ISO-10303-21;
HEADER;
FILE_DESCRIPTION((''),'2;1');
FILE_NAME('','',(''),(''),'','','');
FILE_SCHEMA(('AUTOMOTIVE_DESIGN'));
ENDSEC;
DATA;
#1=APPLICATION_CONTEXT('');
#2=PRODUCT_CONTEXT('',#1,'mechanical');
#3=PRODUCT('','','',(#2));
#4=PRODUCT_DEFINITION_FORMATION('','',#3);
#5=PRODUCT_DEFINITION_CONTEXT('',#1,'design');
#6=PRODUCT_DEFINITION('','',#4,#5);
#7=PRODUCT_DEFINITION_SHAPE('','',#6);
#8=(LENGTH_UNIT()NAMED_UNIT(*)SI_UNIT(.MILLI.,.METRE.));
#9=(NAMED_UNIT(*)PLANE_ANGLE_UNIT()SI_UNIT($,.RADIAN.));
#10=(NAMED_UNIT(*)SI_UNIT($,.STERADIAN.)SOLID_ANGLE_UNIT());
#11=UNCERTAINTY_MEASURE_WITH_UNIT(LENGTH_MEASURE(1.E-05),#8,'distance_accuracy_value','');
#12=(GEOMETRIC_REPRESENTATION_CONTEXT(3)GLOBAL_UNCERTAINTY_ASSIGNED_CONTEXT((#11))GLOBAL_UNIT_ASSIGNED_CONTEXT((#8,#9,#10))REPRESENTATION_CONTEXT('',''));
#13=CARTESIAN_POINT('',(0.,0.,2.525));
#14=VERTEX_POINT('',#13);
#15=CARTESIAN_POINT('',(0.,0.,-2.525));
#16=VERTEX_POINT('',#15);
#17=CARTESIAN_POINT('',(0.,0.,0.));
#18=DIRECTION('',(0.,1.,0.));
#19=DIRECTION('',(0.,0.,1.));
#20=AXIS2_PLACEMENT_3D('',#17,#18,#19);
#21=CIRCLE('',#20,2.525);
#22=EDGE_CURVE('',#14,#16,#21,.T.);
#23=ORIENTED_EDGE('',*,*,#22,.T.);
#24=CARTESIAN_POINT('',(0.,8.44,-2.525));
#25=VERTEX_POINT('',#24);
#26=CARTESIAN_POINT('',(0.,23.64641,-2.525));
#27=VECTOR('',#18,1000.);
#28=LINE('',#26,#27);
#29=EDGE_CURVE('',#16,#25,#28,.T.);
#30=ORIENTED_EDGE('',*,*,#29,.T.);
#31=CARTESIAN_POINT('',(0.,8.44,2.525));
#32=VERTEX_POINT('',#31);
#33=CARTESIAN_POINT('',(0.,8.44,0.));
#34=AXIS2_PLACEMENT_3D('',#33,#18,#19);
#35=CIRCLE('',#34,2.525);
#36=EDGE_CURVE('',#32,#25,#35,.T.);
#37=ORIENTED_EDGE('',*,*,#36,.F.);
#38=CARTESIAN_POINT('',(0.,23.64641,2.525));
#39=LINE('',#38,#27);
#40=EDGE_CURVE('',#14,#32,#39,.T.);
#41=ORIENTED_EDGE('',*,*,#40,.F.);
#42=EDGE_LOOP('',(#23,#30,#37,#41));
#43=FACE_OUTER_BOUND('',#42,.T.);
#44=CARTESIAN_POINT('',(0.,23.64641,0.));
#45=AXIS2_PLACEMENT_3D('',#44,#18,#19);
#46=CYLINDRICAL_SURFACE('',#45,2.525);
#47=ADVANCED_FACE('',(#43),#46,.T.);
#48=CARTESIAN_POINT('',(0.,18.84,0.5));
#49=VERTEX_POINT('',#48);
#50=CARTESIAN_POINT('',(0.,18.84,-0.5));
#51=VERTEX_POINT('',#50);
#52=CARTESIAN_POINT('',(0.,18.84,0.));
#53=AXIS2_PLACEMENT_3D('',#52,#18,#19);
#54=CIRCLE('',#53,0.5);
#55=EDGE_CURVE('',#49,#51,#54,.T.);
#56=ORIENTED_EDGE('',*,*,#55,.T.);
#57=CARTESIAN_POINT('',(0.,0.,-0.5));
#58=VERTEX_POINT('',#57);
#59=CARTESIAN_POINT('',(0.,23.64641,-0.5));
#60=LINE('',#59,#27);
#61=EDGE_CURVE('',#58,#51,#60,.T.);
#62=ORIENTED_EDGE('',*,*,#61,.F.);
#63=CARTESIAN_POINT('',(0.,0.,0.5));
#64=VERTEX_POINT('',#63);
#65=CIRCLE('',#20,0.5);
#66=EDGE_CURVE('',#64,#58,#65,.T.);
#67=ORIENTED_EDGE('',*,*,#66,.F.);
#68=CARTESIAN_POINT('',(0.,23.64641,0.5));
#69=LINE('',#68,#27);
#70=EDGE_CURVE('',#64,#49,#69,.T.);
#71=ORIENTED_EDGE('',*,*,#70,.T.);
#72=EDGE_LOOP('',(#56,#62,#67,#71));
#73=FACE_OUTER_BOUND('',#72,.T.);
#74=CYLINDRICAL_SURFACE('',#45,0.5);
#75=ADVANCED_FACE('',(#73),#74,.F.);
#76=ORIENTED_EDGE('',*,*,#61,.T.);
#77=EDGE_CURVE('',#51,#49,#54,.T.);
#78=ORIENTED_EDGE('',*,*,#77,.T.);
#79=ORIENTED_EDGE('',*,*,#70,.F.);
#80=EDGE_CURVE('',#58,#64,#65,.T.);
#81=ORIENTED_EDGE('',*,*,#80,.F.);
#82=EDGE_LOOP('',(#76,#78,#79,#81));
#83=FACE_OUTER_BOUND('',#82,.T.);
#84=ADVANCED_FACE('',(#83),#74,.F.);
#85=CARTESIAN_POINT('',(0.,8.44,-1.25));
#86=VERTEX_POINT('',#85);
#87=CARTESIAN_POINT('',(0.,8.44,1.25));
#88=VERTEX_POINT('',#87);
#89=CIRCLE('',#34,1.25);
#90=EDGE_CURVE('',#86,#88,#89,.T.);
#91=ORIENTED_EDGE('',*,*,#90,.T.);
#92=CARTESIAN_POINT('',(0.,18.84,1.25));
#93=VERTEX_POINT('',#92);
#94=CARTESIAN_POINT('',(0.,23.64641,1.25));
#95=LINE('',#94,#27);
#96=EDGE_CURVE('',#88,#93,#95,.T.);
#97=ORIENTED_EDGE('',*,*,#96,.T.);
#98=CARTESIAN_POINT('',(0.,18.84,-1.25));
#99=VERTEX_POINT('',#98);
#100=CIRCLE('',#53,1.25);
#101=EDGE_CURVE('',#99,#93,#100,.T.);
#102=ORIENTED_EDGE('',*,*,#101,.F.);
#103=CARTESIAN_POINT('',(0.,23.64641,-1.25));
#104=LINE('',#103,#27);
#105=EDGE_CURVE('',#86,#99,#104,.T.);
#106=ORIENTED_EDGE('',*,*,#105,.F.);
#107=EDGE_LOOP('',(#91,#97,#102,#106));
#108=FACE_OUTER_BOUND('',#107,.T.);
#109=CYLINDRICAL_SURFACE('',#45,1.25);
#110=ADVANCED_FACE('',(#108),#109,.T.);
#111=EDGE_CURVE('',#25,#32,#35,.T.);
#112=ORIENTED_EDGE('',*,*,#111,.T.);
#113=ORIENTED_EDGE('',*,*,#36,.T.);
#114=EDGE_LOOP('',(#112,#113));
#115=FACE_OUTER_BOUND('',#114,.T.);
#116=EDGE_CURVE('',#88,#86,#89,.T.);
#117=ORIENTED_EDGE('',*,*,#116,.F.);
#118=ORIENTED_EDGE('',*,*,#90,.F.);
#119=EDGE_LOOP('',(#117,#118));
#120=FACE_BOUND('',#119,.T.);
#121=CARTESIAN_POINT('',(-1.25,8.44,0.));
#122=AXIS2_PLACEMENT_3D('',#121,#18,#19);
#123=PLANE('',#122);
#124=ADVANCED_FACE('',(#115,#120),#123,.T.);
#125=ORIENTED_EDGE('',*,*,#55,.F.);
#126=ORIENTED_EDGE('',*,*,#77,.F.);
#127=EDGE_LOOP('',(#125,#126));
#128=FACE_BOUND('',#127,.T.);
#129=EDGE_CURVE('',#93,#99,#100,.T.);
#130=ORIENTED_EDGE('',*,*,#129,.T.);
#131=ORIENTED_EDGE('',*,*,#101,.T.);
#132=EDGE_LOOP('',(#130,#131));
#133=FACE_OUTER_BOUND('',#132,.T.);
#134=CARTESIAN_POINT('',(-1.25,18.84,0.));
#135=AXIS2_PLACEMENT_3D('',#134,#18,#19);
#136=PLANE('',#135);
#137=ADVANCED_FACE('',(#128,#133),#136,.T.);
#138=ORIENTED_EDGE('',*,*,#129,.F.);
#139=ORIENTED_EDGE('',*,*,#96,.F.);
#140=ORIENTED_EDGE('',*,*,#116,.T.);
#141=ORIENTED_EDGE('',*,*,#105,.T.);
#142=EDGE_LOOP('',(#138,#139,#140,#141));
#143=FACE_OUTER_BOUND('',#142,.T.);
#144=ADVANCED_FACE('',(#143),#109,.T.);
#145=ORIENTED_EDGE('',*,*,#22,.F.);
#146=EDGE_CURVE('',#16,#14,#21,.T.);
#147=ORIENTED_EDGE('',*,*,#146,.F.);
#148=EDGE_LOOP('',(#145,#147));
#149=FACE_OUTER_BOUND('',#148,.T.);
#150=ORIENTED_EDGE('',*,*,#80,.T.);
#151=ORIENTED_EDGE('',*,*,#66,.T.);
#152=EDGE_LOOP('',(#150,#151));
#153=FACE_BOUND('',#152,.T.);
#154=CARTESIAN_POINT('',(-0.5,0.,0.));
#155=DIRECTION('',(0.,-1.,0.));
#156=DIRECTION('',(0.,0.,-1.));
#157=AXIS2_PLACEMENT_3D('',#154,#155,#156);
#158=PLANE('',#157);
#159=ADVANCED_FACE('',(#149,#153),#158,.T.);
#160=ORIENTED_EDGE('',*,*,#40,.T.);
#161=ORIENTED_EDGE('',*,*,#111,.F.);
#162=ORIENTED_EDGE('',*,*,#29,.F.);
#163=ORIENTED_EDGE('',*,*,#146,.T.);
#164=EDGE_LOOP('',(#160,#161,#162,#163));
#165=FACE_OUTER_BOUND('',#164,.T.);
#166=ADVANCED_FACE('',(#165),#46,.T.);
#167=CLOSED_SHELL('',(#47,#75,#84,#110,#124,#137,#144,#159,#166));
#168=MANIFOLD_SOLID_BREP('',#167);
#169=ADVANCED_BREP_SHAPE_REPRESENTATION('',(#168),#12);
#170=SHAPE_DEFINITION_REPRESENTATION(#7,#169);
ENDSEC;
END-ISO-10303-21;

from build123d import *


with BuildPart() as part:
    # Sketch1 → Revolve2 (revolve)
    with BuildSketch(Plane.XY, mode=Mode.PRIVATE) as revolve2_sk:
        Polygon((-1.25, 8.44), (-1.25, 18.84), (-0.5, 18.84), (-0.5, 0), (-2.525, 0), (-2.525, 8.44), align=None)
    revolve(revolve2_sk.sketch.rotate(Axis((0, 23.646410138, 0), (0, -1, 0)), 270), axis=Axis((0, 23.646410138, 0), (0, -1, 0)))


solid = part.part
